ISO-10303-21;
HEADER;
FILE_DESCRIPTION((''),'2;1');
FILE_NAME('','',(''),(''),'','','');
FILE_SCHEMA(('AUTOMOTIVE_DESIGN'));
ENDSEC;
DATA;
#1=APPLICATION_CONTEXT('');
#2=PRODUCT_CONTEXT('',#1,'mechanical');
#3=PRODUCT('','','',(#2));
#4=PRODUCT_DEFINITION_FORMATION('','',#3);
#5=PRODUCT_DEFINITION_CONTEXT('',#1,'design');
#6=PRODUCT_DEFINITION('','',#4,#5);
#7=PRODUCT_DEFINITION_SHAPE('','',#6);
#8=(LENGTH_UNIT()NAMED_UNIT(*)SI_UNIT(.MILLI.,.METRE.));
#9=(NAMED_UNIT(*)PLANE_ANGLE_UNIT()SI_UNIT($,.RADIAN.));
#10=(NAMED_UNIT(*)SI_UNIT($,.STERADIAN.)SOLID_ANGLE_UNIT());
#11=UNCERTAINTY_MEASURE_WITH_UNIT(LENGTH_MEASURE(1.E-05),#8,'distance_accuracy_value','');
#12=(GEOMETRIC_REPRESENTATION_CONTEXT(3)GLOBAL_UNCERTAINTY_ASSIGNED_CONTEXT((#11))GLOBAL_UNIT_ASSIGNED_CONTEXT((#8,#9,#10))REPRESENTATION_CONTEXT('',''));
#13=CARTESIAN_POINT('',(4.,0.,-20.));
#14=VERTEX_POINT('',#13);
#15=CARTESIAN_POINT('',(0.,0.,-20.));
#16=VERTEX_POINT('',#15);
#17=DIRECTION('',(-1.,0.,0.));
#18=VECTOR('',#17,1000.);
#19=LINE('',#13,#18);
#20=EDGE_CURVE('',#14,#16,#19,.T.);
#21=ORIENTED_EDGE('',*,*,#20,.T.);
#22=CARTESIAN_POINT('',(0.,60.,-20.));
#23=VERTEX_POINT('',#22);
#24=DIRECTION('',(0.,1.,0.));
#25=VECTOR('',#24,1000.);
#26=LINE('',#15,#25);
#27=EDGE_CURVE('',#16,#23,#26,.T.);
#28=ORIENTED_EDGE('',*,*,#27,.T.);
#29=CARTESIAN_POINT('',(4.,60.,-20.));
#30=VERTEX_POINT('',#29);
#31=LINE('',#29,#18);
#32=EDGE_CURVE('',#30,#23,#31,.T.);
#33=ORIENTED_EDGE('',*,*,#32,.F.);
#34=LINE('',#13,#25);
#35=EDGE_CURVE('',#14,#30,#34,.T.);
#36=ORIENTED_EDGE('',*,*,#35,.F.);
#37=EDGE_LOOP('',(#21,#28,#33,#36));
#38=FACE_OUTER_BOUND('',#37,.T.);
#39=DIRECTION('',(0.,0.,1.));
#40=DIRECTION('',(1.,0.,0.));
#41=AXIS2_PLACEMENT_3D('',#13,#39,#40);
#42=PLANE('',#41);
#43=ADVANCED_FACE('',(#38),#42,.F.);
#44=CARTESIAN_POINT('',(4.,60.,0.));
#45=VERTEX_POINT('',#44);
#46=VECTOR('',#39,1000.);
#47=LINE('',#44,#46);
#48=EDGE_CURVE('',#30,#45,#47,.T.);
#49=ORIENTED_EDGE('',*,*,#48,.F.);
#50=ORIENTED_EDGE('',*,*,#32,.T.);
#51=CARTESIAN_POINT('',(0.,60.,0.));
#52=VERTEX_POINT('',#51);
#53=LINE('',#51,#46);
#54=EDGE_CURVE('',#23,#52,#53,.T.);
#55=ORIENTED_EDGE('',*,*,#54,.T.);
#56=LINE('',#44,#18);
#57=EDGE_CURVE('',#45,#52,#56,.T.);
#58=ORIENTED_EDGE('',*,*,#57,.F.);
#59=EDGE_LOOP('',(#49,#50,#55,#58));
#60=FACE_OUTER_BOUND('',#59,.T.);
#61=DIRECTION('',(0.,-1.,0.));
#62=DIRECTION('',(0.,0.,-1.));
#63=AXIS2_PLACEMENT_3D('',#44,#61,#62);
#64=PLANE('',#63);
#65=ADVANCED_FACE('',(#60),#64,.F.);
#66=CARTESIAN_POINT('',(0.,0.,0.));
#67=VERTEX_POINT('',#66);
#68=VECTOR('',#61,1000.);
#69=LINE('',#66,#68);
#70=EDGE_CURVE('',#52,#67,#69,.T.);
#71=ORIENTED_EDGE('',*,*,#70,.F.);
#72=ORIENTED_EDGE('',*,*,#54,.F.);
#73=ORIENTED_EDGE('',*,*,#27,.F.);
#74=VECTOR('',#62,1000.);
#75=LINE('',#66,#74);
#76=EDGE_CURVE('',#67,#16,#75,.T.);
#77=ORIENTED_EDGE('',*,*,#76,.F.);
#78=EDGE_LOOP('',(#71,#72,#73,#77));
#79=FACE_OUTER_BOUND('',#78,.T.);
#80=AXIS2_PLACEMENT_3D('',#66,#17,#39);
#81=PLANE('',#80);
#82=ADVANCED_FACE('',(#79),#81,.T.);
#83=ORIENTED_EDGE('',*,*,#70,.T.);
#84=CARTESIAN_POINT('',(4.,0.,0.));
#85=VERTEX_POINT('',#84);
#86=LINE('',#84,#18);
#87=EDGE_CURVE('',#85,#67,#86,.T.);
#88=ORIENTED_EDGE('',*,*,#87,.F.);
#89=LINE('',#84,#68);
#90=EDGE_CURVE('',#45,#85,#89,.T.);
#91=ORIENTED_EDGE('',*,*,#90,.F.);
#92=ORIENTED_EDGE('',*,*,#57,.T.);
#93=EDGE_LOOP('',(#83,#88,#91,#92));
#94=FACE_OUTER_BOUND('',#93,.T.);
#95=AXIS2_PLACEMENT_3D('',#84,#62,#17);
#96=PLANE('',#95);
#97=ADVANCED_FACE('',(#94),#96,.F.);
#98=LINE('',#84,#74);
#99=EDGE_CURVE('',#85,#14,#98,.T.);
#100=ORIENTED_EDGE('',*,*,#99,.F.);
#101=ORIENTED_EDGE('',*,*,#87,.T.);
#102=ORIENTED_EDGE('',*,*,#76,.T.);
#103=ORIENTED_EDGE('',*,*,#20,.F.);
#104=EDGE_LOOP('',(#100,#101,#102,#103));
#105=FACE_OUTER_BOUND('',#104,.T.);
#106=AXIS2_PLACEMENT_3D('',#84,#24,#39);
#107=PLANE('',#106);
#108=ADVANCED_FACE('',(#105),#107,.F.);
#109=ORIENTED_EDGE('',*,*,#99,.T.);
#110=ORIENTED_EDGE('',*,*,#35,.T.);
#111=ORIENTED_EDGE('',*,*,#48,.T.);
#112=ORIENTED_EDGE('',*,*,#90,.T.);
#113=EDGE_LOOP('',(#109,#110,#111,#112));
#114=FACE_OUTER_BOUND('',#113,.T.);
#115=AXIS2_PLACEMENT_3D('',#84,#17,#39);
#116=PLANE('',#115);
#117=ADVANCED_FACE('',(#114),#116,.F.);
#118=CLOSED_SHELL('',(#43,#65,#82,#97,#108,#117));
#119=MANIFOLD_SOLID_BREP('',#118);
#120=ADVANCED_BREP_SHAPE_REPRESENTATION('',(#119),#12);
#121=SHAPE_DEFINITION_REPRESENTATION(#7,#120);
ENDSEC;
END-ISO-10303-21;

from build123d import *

# Parameters (mm, degrees)
SKETCH_1_W      = 20
SKETCH_1_H      = 60
EXTRUDE_1_DEPTH = 4


with BuildPart() as part:
    # 草图1 → 凸台-拉伸1 (new body)
    with BuildSketch(Plane(origin=(0, 0, 0), x_dir=(0, 0, -1), z_dir=(1, 0, 0))):
        with Locations((10, 30)):
            Rectangle(SKETCH_1_W, SKETCH_1_H)
    extrude(amount=EXTRUDE_1_DEPTH)


solid = part.part
